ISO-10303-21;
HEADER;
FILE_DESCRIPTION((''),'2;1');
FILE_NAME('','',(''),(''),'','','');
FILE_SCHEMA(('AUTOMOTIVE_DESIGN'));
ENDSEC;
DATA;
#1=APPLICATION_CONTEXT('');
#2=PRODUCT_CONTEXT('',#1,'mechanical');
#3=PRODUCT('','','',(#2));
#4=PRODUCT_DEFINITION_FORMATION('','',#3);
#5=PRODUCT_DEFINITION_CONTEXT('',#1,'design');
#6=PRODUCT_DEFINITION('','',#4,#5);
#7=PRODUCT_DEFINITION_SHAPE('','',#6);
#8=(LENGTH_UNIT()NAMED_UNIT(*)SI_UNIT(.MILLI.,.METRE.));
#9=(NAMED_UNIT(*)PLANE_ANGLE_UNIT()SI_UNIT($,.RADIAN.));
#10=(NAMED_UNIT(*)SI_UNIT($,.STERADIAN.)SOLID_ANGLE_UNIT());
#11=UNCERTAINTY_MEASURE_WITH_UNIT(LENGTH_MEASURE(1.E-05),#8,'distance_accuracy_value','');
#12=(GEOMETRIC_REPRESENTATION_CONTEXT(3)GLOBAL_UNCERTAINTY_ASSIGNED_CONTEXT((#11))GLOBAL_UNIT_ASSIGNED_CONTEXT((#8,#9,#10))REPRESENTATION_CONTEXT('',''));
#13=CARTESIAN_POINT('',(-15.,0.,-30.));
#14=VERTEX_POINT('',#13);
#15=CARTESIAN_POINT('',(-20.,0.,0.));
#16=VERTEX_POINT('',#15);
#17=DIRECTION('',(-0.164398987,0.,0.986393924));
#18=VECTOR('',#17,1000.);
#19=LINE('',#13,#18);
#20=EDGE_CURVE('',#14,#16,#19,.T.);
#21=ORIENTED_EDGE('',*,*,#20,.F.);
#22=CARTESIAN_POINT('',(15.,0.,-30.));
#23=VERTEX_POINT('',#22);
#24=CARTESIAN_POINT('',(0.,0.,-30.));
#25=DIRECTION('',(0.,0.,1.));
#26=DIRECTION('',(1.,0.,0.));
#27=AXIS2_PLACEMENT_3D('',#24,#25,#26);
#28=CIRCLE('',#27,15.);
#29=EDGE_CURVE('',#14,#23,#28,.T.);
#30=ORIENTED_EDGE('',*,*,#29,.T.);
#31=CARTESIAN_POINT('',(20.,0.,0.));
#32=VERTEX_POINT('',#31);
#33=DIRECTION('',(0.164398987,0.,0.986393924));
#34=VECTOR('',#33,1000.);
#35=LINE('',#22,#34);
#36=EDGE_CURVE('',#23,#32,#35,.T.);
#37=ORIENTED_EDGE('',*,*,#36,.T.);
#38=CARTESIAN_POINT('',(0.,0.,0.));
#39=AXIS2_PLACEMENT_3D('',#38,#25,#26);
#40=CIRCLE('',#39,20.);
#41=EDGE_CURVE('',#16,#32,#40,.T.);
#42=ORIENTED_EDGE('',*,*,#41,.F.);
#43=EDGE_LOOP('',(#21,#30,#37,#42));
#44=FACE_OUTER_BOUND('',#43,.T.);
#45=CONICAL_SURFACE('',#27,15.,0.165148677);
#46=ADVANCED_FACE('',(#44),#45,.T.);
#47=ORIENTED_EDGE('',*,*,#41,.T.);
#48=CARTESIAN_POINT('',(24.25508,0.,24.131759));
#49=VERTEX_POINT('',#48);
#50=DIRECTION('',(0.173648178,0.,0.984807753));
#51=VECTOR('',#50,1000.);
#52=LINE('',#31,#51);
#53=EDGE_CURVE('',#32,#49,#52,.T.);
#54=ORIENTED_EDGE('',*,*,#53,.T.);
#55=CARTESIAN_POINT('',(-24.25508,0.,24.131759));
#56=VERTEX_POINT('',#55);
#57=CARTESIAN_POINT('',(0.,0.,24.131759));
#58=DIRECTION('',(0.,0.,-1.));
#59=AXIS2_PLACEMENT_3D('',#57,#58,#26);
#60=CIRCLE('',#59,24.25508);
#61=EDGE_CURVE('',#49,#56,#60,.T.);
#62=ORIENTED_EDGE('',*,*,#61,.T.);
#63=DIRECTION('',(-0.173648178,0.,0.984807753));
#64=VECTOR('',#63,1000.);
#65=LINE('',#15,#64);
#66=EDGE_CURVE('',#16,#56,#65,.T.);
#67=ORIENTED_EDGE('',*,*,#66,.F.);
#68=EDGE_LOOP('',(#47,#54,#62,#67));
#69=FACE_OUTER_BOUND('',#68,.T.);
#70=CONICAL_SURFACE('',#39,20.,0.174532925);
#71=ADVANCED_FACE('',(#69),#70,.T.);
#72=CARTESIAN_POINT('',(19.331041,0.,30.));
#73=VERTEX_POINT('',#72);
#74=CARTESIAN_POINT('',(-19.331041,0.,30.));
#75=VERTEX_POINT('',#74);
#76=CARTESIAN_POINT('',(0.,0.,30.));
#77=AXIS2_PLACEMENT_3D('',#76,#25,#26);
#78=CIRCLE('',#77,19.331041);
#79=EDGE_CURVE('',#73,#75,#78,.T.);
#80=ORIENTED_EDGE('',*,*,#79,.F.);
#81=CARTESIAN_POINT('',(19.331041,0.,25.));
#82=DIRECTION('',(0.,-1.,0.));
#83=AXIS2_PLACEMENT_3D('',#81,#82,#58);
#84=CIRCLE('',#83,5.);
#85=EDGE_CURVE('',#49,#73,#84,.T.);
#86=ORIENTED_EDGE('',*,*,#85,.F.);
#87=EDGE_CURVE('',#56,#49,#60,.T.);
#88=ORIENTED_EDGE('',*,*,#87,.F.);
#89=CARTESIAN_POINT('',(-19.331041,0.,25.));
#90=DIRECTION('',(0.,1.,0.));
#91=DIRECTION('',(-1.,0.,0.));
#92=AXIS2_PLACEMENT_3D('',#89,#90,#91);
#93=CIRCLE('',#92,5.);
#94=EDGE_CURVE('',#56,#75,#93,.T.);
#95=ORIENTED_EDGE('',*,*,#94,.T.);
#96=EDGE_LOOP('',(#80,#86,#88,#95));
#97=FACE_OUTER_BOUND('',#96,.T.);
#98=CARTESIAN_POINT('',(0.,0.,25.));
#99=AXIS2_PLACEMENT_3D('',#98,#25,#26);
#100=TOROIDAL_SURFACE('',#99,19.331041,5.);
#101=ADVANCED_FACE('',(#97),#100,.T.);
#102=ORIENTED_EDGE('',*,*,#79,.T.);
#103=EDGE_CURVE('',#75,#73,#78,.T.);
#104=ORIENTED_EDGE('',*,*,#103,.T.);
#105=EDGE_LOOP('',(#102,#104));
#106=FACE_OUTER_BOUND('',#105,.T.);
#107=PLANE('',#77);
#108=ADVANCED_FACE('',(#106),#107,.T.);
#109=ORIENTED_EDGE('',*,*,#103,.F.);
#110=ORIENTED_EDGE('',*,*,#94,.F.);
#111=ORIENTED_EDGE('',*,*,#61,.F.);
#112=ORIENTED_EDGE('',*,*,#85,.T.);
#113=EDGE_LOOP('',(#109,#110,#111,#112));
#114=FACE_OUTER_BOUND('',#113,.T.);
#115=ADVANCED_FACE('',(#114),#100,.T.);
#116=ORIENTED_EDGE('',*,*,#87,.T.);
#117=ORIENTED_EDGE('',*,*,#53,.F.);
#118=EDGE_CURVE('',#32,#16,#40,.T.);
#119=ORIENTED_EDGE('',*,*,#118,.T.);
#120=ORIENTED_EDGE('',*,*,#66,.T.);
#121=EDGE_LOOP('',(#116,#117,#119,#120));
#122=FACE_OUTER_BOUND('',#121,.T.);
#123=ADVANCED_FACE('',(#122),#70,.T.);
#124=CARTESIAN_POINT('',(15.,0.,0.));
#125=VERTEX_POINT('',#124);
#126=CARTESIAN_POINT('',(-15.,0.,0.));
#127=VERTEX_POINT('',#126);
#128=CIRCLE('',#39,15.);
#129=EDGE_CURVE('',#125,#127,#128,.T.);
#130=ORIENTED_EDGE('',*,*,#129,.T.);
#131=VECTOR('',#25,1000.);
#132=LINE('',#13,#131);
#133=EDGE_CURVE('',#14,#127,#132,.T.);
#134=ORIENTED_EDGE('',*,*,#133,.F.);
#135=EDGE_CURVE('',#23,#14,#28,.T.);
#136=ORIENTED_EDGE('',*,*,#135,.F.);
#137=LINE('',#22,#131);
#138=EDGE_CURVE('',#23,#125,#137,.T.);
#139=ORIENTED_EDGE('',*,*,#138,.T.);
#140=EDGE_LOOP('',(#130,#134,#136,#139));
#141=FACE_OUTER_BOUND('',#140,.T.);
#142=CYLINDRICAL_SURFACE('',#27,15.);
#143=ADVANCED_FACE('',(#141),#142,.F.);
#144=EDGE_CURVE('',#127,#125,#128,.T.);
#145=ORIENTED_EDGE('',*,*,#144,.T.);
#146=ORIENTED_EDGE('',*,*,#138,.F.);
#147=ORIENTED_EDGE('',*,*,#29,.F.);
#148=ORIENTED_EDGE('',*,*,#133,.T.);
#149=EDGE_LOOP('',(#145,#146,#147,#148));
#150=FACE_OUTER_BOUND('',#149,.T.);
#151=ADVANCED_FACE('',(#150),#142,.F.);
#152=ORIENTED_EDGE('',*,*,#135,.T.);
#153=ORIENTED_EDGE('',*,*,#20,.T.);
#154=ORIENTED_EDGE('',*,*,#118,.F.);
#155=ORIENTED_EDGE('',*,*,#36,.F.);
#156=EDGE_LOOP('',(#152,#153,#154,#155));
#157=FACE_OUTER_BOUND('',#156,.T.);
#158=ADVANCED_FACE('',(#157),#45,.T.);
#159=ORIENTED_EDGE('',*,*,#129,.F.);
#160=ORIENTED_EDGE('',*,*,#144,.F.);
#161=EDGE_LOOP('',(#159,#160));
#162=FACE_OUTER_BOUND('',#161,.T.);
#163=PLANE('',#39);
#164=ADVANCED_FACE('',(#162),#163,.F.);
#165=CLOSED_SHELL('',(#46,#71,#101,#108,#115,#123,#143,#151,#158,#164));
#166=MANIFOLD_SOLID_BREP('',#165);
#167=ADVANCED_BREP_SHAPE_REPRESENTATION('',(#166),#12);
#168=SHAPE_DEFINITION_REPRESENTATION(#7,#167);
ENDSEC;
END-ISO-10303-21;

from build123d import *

# Parameters (mm, degrees)
SKETCH_1_3_R        = 20
BOSS_EXTRUDE1_DEPTH = 30
BOSS_EXTRUDE1_DRAFT = -10
SKETCH_1_3_2_R      = 20
SKETCH_1_3_2_R_2    = 15
BOSS_EXTRUDE2_DEPTH = 30
FILLET1_R           = 5


with BuildPart() as part:
    # Sketch 1_3 → Boss-Extrude1 (with draft: the straight prism first)
    with BuildSketch(Plane.XY):
        Circle(SKETCH_1_3_R)
    extrude(amount=BOSS_EXTRUDE1_DEPTH)
    # Boss-Extrude1: the draft: its side faces are tilted about the plane it starts from
    boss_extrude1_sides = [part.faces().sort_by_distance(p)[0] for p in [
        (-20, 0, 15),
    ]]
    draft(boss_extrude1_sides, Plane.XY, BOSS_EXTRUDE1_DRAFT)

    # Sketch 1_3 2 → Boss-Extrude2 (add)
    with BuildSketch(Plane.XY):
        Circle(SKETCH_1_3_2_R)
        Circle(SKETCH_1_3_2_R_2, mode=Mode.SUBTRACT)
    extrude(amount=-BOSS_EXTRUDE2_DEPTH)

    # Sketch2 → Cut-Revolve1 (revolve, cut)
    with BuildSketch(Plane(origin=(0, 0, 0), x_dir=(1, 0, 0), z_dir=(0, 1, 0))):
        Polygon((20, 0), (15, 30), (20, 30), align=None)
    revolve(axis=Axis((0, 0, 0), (0, 0, -1)), mode=Mode.SUBTRACT)

    # Fillet1
    fillet1_edges = [part.edges().sort_by_distance(p)[0] for p in [
        (-25.289809421, 0, 30),
    ]]
    fillet(fillet1_edges, radius=FILLET1_R)


solid = part.part
